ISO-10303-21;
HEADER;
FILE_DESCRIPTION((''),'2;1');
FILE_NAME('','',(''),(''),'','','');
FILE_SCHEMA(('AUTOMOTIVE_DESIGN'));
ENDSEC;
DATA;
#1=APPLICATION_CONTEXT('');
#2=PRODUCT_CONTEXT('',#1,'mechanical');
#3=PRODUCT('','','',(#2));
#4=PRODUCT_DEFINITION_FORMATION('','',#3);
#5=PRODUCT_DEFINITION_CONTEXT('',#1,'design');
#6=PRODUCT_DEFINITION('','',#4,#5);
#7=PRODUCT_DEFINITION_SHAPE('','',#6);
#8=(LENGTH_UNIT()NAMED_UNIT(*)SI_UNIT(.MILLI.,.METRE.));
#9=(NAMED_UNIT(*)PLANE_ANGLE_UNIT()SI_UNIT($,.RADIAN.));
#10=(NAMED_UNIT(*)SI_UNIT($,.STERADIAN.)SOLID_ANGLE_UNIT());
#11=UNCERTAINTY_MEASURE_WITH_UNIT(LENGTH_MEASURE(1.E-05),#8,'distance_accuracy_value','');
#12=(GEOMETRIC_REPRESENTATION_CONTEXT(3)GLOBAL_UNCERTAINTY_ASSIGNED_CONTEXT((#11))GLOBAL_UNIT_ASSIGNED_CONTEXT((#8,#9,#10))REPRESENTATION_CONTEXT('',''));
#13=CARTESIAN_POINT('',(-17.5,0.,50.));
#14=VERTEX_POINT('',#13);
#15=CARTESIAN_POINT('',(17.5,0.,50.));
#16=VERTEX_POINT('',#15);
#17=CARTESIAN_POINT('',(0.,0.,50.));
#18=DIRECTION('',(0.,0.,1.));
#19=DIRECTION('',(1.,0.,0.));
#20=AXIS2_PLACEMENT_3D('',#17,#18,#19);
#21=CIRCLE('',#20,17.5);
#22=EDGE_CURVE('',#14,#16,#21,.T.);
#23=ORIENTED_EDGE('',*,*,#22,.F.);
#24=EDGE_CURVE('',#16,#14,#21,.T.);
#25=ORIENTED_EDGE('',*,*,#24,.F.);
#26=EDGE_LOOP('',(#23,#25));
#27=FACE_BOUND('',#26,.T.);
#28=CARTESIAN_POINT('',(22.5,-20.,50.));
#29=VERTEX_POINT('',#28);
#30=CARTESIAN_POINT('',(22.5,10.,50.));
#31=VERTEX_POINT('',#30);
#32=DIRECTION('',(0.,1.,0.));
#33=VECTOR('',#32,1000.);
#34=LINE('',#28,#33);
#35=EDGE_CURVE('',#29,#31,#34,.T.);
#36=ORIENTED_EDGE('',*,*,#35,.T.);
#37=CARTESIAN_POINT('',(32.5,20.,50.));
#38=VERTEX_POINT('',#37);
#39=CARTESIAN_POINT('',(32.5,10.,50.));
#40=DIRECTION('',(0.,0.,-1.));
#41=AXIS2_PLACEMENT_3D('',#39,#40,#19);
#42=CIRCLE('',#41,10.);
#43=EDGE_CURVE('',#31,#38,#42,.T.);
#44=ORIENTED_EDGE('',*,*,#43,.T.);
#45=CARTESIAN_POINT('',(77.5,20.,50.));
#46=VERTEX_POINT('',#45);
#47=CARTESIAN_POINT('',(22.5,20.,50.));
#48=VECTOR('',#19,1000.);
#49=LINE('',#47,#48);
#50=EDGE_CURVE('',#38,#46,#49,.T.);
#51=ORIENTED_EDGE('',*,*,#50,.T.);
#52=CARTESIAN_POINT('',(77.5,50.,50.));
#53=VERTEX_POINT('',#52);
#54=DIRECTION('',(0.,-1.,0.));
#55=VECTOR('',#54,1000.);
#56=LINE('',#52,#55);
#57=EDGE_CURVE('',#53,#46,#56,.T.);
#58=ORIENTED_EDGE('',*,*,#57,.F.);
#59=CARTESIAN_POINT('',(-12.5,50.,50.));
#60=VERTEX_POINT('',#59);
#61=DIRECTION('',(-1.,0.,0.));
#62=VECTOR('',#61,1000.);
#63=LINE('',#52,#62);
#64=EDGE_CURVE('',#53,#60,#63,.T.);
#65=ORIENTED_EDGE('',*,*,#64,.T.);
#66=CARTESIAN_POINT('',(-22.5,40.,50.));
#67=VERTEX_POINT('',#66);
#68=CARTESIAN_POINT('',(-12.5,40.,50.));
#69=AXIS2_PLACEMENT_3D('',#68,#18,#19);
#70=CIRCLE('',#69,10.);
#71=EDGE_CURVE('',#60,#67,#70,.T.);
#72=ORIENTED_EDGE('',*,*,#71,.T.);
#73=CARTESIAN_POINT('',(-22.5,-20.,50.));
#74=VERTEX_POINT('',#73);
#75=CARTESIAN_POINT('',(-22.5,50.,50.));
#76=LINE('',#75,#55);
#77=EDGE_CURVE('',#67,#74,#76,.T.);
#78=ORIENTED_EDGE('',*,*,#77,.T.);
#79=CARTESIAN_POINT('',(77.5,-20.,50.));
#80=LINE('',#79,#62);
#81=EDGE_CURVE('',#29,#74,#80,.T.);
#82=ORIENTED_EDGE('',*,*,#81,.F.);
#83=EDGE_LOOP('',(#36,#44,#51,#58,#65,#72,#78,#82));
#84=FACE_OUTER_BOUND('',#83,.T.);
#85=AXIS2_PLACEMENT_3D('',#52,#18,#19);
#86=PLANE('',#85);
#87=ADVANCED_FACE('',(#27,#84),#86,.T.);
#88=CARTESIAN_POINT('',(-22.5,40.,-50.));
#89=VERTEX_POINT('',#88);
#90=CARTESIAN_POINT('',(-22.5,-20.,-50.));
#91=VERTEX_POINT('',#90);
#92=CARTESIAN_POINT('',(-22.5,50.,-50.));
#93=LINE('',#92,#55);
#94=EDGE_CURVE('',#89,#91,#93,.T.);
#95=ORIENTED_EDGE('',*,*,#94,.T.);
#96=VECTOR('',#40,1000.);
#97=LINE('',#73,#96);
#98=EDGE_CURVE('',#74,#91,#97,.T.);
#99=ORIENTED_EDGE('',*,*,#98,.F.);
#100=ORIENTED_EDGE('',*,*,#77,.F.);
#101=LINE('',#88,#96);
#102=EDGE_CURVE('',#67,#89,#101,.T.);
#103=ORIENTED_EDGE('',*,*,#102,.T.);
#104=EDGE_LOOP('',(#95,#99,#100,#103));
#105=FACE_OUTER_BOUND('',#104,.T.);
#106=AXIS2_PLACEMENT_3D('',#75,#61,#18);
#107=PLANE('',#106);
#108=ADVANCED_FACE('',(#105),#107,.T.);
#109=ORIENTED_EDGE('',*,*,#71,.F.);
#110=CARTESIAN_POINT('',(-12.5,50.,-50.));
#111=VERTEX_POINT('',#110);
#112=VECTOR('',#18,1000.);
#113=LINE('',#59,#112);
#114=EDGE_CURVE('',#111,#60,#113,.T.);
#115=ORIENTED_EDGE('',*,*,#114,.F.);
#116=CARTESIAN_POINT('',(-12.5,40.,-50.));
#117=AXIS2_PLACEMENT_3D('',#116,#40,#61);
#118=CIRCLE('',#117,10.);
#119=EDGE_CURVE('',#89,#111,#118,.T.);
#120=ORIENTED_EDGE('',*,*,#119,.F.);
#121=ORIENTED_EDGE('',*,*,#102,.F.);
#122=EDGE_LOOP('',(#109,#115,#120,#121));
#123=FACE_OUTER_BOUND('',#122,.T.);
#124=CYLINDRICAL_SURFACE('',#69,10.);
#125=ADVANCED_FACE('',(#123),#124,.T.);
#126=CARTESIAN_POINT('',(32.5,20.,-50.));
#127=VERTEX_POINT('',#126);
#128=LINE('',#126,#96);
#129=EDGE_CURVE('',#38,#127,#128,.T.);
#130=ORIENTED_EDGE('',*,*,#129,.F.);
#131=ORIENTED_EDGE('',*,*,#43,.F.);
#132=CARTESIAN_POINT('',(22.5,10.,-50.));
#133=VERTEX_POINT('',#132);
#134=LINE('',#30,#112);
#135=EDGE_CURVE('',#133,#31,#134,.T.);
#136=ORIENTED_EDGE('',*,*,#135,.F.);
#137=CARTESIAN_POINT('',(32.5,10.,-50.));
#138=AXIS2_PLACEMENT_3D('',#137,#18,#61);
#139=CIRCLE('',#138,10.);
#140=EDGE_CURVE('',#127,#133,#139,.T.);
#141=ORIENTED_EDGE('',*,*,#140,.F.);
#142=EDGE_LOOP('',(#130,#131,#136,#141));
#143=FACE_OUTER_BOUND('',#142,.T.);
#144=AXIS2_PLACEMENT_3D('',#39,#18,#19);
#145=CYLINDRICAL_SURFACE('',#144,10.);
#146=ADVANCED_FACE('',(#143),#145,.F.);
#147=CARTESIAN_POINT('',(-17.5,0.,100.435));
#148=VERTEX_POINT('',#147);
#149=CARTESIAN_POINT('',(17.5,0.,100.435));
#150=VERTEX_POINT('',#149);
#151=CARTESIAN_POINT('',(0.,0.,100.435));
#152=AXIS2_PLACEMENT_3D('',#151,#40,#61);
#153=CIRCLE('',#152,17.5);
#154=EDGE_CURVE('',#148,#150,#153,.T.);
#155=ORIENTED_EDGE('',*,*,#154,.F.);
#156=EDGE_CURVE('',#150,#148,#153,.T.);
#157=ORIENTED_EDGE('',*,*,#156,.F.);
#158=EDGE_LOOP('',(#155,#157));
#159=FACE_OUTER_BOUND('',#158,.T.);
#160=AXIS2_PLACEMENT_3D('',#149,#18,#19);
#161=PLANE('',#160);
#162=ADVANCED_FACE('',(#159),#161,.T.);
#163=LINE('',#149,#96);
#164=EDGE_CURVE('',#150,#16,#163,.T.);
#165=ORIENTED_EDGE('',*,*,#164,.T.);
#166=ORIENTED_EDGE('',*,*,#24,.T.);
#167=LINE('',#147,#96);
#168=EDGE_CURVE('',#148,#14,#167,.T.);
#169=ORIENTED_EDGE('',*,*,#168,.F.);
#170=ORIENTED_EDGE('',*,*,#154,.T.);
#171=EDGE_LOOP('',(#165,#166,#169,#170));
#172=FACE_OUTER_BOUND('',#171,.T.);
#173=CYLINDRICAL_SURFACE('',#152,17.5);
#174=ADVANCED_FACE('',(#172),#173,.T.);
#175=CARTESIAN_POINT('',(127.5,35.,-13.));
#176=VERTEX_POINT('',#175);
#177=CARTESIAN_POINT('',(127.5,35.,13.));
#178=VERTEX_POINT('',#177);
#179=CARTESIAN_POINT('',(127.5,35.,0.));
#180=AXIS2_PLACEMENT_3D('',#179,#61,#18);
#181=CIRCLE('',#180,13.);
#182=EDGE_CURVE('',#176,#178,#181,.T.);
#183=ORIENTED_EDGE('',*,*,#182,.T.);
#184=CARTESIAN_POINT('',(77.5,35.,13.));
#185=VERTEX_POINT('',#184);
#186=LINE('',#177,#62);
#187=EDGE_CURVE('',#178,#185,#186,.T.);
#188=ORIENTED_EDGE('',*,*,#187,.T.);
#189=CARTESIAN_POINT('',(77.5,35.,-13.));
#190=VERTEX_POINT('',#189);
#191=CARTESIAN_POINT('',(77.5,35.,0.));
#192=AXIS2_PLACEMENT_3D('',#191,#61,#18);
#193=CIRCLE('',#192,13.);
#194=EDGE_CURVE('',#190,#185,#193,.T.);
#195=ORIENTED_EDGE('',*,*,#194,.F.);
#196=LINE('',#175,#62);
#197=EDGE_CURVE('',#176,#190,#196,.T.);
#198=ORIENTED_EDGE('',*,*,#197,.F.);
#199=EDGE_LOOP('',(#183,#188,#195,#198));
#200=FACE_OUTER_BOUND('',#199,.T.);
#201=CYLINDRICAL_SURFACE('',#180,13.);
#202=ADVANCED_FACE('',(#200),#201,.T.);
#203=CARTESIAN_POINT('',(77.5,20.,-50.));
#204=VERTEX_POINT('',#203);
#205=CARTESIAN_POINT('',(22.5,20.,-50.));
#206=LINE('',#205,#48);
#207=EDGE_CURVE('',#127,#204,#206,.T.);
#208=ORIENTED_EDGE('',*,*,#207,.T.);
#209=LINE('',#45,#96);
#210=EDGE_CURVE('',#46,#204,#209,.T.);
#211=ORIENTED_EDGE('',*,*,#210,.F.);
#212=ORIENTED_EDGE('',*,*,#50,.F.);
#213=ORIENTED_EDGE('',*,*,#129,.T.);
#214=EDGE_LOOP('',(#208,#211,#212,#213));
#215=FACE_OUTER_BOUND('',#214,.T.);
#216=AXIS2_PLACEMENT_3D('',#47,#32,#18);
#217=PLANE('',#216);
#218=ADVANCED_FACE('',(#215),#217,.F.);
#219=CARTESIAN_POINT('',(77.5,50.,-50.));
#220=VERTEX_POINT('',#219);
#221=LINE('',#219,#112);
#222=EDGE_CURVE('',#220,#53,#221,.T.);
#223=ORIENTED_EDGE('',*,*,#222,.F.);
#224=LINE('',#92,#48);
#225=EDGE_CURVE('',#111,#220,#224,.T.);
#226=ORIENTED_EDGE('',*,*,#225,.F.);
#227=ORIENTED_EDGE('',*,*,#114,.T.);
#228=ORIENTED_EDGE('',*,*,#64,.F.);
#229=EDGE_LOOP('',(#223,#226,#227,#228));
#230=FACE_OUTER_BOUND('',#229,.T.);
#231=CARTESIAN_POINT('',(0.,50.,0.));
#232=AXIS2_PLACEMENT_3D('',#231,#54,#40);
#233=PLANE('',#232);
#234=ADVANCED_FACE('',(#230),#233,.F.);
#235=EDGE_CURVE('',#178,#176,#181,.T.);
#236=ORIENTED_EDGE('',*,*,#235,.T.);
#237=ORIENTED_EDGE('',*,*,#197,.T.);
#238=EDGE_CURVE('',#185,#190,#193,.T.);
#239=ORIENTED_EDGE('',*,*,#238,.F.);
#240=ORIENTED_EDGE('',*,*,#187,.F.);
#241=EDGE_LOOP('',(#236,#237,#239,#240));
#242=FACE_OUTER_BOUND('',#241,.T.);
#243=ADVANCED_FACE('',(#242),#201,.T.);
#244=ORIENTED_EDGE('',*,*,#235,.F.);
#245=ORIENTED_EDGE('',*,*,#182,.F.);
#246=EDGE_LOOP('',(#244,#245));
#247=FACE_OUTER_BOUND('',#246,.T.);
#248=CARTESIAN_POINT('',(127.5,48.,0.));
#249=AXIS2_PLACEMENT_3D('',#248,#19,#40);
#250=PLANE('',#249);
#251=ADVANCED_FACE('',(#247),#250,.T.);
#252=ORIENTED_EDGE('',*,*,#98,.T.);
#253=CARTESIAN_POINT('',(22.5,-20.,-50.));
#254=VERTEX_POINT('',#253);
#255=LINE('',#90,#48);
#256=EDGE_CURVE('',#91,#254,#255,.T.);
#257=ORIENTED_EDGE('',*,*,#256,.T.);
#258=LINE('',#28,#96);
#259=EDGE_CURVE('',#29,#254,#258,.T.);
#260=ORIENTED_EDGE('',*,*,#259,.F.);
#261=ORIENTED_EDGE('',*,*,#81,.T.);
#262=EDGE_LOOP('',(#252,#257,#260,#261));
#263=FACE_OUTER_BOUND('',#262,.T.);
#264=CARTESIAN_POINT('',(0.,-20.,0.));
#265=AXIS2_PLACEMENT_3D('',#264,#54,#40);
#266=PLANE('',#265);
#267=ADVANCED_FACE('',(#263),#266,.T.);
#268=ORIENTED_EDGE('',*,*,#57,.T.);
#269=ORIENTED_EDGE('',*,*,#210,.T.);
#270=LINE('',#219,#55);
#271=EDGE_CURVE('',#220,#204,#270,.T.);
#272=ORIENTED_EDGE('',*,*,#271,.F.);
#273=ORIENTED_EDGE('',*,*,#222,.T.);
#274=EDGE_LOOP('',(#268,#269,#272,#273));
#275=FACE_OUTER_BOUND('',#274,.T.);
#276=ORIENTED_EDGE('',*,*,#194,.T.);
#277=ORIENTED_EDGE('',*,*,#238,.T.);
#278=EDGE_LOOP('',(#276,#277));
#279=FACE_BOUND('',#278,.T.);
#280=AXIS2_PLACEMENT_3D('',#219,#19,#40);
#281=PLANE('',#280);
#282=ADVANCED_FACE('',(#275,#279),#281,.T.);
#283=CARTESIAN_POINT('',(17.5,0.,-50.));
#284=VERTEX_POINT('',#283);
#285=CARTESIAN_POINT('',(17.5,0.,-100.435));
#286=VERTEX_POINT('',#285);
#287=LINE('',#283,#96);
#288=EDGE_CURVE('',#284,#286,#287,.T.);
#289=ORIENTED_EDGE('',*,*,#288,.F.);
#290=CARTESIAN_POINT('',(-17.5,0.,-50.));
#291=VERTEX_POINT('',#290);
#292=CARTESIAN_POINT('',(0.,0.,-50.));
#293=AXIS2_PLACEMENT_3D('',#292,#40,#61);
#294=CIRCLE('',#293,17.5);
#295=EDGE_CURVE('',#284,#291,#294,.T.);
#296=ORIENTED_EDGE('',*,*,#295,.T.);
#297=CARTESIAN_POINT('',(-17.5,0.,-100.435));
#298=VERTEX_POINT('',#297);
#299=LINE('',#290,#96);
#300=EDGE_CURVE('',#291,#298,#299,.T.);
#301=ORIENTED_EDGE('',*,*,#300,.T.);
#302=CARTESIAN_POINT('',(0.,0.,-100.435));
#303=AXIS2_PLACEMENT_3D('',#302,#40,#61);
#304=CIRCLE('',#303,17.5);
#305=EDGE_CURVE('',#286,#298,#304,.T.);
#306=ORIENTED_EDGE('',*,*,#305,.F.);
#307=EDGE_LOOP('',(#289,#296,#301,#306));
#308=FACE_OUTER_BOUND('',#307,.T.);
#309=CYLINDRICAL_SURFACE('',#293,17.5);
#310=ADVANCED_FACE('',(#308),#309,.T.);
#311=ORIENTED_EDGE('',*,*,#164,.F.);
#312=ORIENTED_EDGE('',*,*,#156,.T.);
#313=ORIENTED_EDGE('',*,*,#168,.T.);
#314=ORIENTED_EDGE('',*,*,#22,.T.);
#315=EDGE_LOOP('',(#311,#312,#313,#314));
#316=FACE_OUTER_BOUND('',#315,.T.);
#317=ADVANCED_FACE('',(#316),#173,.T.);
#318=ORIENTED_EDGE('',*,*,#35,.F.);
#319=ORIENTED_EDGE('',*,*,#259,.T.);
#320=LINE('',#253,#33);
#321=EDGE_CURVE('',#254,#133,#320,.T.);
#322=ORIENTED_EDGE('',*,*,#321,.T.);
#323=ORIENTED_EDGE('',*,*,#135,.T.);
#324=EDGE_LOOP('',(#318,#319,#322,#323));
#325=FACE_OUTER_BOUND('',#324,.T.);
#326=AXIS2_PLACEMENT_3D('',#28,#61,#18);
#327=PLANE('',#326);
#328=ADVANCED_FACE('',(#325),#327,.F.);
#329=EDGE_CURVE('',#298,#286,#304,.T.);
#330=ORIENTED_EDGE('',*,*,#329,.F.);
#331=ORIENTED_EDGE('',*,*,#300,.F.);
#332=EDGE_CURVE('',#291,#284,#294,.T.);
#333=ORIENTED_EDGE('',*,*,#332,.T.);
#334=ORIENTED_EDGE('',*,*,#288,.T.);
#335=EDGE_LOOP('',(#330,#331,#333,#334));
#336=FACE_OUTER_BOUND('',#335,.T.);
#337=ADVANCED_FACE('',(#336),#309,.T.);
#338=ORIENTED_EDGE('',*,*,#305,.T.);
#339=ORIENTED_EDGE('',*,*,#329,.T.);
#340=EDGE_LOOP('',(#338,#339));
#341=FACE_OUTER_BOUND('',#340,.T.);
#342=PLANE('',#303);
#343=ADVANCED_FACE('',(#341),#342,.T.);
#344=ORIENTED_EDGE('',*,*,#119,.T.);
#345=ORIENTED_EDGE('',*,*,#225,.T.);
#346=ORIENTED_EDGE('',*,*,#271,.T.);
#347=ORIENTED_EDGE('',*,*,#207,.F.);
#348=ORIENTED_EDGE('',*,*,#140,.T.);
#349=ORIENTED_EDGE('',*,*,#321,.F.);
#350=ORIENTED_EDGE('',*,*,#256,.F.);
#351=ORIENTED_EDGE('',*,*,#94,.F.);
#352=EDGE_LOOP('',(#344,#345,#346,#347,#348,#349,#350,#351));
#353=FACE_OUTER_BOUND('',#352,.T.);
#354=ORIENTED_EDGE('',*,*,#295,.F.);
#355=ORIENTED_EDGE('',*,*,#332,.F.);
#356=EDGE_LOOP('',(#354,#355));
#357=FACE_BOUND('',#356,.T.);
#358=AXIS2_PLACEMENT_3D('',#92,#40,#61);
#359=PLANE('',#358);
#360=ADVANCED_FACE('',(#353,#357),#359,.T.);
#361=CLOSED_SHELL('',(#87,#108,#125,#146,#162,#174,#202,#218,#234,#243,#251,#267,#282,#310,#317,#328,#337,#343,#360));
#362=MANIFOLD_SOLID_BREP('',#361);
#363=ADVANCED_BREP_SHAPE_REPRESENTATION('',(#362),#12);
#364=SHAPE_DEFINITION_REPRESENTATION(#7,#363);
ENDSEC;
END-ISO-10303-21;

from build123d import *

# Parameters (mm, degrees)
SKETCH1_W           = 100
SKETCH1_H           = 100
BOSS_EXTRUDE1_DEPTH = 70
SKETCH2_W           = 55
SKETCH2_H           = 40
CUT_EXTRUDE1_DEPTH  = 137.037678604
SKETCH3_W           = 50
SKETCH3_H           = 13
SKETCH4_W           = 17.5
SKETCH4_H           = 50.435
SKETCH5_W           = 17.5
SKETCH5_H           = 50.435
FILLET1_R           = 10


with BuildPart() as part:
    # Sketch1 → Boss-Extrude1 (new body)
    with BuildSketch(Plane.XZ.offset(20)):
        with Locations((27.5, 0)):
            Rectangle(SKETCH1_W, SKETCH1_H)
    extrude(amount=-BOSS_EXTRUDE1_DEPTH)

    # Sketch2 → Cut-Extrude1 (cut, through all)
    with BuildSketch(Plane(origin=(0, 0, -50), x_dir=(-1, 0, 0), z_dir=(0, 0, -1))):
        with Locations((-50, 0)):
            Rectangle(SKETCH2_W, SKETCH2_H)
    extrude(amount=-CUT_EXTRUDE1_DEPTH, mode=Mode.SUBTRACT)

    # Sketch3 → Revolve1 (revolve)
    with BuildSketch(Plane(origin=(0, 0, 0), x_dir=(-1, 0, 0), z_dir=(0, 0, -1)), mode=Mode.PRIVATE) as revolve1_sk:
        with Locations((-102.5, 41.5)):
            Rectangle(SKETCH3_W, SKETCH3_H)
    revolve(revolve1_sk.sketch.rotate(Axis((127.5, 35, 0), (-1, 0, 0)), 270), axis=Axis((127.5, 35, 0), (-1, 0, 0)))

    # Sketch4 → Revolve2 (revolve)
    with BuildSketch(Plane.XZ, mode=Mode.PRIVATE) as revolve2_sk:
        with Locations((8.75, -75.2175)):
            Rectangle(SKETCH4_W, SKETCH4_H)
    revolve(revolve2_sk.sketch.rotate(Axis((0, 0, -50), (0, 0, -1)), 180), axis=Axis((0, 0, -50), (0, 0, -1)))

    # Sketch5 → Revolve3 (revolve)
    with BuildSketch(Plane.XZ, mode=Mode.PRIVATE) as revolve3_sk:
        with Locations((8.75, 75.2175)):
            Rectangle(SKETCH5_W, SKETCH5_H)
    revolve(revolve3_sk.sketch.rotate(Axis((0, 0, 100.435), (0, 0, -1)), 180), axis=Axis((0, 0, 100.435), (0, 0, -1)))

    # Fillet1
    fillet1_edges = [part.edges().sort_by_distance(p)[0] for p in [
        (22.5, 20, 0),
        (-22.5, 50, 0),
    ]]
    fillet(fillet1_edges, radius=FILLET1_R)


solid = part.part
